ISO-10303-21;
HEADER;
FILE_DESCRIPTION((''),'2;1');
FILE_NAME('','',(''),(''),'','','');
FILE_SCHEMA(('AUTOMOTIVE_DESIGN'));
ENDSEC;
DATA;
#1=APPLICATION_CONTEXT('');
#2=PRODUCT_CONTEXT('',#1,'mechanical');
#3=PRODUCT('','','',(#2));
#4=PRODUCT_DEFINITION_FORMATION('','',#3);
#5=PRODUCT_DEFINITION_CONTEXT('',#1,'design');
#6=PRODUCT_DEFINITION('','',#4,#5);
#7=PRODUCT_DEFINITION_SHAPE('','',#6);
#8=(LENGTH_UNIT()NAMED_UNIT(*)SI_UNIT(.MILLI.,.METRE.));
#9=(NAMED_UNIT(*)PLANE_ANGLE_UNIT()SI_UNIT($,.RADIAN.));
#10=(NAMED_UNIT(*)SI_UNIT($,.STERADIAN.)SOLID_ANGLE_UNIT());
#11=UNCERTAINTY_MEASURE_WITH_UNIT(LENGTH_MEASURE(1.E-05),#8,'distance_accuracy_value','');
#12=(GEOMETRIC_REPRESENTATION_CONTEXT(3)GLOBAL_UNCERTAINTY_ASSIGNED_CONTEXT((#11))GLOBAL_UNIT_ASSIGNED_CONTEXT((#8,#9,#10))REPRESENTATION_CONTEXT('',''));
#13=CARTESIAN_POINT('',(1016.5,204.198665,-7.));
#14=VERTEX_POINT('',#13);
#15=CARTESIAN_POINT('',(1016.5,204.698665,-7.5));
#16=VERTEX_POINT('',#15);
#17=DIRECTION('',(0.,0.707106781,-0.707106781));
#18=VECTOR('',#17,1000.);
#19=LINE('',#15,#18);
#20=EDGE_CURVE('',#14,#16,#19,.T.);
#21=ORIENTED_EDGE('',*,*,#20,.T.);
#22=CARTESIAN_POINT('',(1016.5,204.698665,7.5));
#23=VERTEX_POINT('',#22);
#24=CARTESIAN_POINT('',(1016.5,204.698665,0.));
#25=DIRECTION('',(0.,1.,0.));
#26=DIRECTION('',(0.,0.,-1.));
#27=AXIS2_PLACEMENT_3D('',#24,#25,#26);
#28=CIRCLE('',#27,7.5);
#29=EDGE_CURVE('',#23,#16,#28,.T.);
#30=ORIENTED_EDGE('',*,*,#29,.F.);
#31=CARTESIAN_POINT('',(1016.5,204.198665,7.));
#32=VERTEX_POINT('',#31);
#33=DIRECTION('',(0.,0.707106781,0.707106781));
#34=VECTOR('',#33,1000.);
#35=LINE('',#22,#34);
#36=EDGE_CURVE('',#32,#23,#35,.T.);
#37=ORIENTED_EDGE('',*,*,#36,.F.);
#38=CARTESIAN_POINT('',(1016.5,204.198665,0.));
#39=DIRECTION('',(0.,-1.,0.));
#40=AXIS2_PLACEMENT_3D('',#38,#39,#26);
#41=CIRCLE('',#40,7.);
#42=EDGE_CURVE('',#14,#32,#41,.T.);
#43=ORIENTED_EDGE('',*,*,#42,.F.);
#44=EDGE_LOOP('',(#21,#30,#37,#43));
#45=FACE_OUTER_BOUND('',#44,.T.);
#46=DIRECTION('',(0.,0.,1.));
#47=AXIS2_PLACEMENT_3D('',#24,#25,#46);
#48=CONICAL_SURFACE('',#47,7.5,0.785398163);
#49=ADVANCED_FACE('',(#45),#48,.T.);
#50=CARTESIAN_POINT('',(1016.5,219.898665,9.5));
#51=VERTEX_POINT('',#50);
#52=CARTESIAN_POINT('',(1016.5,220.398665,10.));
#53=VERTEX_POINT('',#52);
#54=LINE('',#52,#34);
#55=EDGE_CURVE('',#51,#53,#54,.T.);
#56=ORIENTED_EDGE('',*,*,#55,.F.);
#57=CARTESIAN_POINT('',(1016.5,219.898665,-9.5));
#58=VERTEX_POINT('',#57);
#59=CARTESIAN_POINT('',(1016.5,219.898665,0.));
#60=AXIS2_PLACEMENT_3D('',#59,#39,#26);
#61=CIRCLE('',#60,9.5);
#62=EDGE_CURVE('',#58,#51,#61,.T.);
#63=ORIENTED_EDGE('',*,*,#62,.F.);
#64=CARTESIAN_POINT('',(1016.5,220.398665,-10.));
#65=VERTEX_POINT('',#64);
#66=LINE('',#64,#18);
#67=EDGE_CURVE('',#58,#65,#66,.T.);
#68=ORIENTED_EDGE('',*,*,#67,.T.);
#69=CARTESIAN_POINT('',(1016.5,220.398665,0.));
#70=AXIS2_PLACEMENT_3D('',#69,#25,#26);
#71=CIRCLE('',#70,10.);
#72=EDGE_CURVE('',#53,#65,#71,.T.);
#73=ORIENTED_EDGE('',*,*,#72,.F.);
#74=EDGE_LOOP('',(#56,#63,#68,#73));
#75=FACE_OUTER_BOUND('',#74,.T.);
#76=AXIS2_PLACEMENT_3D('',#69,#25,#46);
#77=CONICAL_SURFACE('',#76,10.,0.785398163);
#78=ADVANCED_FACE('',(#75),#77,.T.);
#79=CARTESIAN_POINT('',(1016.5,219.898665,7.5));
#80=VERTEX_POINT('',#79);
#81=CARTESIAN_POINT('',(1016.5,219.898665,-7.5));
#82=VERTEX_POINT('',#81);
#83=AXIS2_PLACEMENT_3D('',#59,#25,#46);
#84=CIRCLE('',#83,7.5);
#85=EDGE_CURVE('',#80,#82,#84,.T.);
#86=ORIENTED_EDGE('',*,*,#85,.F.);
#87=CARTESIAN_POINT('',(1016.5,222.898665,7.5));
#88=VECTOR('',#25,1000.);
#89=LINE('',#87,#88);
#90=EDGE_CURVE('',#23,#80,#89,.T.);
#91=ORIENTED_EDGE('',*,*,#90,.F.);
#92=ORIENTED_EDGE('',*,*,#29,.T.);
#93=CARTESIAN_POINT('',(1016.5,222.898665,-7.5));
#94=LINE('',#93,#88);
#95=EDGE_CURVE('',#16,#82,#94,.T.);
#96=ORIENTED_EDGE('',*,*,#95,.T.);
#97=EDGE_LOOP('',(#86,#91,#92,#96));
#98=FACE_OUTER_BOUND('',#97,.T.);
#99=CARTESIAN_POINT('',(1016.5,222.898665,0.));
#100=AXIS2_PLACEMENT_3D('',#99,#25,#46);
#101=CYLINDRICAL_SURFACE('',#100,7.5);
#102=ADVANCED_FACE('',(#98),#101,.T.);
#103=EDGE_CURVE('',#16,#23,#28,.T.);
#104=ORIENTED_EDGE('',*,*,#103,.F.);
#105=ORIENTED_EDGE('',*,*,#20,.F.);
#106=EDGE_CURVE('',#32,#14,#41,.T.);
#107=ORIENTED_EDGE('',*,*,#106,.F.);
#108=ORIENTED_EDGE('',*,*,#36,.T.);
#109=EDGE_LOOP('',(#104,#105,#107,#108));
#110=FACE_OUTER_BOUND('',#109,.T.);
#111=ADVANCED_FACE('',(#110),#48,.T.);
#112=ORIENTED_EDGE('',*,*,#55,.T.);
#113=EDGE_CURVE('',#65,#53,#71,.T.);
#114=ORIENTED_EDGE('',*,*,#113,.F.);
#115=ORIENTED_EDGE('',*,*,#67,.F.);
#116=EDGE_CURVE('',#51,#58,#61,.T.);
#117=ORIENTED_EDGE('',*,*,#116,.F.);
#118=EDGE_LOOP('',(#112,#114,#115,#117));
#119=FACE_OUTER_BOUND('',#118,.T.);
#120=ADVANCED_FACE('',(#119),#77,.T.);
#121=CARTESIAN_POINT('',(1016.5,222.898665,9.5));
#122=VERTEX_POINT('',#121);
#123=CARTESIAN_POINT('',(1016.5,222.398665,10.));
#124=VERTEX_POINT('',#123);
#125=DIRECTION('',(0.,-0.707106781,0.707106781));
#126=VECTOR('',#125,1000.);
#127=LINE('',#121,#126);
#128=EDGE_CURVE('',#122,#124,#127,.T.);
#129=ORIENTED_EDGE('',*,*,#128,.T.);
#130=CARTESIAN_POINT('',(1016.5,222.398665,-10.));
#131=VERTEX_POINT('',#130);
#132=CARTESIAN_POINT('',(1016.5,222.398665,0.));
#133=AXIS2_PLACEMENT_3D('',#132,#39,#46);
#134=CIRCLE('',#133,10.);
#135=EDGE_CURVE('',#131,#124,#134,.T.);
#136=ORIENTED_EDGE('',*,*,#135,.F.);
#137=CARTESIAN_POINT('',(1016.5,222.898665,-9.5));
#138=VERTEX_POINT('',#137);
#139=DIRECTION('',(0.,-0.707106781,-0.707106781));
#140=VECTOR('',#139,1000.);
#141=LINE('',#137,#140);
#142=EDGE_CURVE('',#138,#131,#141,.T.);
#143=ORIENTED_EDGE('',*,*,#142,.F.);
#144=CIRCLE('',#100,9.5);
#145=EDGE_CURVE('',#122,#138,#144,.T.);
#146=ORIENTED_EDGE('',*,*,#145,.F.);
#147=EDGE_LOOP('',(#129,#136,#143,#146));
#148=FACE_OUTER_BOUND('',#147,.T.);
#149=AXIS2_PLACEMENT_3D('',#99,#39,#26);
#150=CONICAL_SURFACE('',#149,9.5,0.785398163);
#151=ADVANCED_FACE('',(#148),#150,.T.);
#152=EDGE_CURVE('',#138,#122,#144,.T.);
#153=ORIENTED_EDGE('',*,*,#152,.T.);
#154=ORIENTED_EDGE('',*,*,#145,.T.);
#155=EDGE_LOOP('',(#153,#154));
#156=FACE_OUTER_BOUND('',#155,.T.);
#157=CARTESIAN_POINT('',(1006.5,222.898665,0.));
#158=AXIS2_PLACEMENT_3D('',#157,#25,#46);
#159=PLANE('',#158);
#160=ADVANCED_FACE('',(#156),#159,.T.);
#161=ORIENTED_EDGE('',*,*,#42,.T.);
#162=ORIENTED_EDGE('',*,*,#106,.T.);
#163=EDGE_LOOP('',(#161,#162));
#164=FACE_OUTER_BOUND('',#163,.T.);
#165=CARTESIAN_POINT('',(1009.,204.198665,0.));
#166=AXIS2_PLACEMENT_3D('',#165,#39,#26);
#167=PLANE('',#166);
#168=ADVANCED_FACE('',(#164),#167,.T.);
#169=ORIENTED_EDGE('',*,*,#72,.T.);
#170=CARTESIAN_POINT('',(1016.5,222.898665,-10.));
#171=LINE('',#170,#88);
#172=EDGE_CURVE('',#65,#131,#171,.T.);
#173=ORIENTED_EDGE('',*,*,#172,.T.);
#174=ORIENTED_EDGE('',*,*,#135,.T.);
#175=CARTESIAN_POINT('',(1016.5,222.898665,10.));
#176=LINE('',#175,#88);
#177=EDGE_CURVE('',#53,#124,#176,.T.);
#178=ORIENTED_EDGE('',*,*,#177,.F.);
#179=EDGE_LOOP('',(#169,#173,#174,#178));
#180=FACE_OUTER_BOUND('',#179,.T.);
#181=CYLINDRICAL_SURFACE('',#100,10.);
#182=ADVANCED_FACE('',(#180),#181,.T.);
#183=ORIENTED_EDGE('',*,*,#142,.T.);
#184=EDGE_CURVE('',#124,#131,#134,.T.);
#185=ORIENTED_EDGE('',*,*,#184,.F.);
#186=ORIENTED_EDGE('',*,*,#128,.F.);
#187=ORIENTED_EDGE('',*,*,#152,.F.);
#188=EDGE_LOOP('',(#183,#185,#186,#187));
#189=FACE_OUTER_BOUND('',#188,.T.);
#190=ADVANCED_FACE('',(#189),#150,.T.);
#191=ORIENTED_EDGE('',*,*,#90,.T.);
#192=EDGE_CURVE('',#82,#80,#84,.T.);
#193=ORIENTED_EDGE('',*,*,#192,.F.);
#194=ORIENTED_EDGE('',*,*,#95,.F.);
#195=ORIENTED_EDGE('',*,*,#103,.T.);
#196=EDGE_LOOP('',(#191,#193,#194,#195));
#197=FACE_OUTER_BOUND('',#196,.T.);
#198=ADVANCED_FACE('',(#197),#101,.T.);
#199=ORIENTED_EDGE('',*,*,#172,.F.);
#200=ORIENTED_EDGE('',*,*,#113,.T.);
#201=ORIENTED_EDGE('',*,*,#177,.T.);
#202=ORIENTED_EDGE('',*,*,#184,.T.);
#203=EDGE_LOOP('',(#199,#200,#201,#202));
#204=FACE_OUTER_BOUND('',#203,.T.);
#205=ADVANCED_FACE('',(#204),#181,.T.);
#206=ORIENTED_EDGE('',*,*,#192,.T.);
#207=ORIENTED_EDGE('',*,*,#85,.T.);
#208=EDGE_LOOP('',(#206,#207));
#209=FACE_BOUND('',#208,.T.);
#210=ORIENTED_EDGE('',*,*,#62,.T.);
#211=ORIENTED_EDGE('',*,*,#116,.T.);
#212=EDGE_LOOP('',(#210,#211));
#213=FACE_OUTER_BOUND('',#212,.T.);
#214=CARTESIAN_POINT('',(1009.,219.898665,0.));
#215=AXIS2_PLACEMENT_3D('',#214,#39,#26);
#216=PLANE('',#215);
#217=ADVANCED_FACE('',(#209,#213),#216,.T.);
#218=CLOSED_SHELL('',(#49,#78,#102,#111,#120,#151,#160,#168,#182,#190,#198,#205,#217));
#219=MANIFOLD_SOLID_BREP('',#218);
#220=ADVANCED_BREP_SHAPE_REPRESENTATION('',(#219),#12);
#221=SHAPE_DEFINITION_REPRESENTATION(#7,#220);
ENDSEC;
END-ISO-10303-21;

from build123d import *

# Parameters (mm, degrees)
CHAMFER1_SIZE = 0.5


with BuildPart() as part:
    # Sketch1 → Revolve1 (revolve)
    with BuildSketch(Plane.XY, mode=Mode.PRIVATE) as revolve1_sk:
        Polygon((1009, 204.198665167), (1009, 219.898665167), (1006.5, 219.898665167), (1006.5, 222.898665167), (1016.5, 222.898665167), (1016.5, 204.198665167), align=None)
    revolve(revolve1_sk.sketch.rotate(Axis((1016.5, 222.898665167, 0), (0, -1, 0)), 270), axis=Axis((1016.5, 222.898665167, 0), (0, -1, 0)))

    # Chamfer1
    chamfer1_edges = [part.edges().sort_by_distance(p)[0] for p in [
        (1016.5, 222.898665167, -10),
        (1016.5, 219.898665167, -10),
        (1016.5, 204.198665167, -7.5),
    ]]
    chamfer(chamfer1_edges, length=CHAMFER1_SIZE)


solid = part.part
